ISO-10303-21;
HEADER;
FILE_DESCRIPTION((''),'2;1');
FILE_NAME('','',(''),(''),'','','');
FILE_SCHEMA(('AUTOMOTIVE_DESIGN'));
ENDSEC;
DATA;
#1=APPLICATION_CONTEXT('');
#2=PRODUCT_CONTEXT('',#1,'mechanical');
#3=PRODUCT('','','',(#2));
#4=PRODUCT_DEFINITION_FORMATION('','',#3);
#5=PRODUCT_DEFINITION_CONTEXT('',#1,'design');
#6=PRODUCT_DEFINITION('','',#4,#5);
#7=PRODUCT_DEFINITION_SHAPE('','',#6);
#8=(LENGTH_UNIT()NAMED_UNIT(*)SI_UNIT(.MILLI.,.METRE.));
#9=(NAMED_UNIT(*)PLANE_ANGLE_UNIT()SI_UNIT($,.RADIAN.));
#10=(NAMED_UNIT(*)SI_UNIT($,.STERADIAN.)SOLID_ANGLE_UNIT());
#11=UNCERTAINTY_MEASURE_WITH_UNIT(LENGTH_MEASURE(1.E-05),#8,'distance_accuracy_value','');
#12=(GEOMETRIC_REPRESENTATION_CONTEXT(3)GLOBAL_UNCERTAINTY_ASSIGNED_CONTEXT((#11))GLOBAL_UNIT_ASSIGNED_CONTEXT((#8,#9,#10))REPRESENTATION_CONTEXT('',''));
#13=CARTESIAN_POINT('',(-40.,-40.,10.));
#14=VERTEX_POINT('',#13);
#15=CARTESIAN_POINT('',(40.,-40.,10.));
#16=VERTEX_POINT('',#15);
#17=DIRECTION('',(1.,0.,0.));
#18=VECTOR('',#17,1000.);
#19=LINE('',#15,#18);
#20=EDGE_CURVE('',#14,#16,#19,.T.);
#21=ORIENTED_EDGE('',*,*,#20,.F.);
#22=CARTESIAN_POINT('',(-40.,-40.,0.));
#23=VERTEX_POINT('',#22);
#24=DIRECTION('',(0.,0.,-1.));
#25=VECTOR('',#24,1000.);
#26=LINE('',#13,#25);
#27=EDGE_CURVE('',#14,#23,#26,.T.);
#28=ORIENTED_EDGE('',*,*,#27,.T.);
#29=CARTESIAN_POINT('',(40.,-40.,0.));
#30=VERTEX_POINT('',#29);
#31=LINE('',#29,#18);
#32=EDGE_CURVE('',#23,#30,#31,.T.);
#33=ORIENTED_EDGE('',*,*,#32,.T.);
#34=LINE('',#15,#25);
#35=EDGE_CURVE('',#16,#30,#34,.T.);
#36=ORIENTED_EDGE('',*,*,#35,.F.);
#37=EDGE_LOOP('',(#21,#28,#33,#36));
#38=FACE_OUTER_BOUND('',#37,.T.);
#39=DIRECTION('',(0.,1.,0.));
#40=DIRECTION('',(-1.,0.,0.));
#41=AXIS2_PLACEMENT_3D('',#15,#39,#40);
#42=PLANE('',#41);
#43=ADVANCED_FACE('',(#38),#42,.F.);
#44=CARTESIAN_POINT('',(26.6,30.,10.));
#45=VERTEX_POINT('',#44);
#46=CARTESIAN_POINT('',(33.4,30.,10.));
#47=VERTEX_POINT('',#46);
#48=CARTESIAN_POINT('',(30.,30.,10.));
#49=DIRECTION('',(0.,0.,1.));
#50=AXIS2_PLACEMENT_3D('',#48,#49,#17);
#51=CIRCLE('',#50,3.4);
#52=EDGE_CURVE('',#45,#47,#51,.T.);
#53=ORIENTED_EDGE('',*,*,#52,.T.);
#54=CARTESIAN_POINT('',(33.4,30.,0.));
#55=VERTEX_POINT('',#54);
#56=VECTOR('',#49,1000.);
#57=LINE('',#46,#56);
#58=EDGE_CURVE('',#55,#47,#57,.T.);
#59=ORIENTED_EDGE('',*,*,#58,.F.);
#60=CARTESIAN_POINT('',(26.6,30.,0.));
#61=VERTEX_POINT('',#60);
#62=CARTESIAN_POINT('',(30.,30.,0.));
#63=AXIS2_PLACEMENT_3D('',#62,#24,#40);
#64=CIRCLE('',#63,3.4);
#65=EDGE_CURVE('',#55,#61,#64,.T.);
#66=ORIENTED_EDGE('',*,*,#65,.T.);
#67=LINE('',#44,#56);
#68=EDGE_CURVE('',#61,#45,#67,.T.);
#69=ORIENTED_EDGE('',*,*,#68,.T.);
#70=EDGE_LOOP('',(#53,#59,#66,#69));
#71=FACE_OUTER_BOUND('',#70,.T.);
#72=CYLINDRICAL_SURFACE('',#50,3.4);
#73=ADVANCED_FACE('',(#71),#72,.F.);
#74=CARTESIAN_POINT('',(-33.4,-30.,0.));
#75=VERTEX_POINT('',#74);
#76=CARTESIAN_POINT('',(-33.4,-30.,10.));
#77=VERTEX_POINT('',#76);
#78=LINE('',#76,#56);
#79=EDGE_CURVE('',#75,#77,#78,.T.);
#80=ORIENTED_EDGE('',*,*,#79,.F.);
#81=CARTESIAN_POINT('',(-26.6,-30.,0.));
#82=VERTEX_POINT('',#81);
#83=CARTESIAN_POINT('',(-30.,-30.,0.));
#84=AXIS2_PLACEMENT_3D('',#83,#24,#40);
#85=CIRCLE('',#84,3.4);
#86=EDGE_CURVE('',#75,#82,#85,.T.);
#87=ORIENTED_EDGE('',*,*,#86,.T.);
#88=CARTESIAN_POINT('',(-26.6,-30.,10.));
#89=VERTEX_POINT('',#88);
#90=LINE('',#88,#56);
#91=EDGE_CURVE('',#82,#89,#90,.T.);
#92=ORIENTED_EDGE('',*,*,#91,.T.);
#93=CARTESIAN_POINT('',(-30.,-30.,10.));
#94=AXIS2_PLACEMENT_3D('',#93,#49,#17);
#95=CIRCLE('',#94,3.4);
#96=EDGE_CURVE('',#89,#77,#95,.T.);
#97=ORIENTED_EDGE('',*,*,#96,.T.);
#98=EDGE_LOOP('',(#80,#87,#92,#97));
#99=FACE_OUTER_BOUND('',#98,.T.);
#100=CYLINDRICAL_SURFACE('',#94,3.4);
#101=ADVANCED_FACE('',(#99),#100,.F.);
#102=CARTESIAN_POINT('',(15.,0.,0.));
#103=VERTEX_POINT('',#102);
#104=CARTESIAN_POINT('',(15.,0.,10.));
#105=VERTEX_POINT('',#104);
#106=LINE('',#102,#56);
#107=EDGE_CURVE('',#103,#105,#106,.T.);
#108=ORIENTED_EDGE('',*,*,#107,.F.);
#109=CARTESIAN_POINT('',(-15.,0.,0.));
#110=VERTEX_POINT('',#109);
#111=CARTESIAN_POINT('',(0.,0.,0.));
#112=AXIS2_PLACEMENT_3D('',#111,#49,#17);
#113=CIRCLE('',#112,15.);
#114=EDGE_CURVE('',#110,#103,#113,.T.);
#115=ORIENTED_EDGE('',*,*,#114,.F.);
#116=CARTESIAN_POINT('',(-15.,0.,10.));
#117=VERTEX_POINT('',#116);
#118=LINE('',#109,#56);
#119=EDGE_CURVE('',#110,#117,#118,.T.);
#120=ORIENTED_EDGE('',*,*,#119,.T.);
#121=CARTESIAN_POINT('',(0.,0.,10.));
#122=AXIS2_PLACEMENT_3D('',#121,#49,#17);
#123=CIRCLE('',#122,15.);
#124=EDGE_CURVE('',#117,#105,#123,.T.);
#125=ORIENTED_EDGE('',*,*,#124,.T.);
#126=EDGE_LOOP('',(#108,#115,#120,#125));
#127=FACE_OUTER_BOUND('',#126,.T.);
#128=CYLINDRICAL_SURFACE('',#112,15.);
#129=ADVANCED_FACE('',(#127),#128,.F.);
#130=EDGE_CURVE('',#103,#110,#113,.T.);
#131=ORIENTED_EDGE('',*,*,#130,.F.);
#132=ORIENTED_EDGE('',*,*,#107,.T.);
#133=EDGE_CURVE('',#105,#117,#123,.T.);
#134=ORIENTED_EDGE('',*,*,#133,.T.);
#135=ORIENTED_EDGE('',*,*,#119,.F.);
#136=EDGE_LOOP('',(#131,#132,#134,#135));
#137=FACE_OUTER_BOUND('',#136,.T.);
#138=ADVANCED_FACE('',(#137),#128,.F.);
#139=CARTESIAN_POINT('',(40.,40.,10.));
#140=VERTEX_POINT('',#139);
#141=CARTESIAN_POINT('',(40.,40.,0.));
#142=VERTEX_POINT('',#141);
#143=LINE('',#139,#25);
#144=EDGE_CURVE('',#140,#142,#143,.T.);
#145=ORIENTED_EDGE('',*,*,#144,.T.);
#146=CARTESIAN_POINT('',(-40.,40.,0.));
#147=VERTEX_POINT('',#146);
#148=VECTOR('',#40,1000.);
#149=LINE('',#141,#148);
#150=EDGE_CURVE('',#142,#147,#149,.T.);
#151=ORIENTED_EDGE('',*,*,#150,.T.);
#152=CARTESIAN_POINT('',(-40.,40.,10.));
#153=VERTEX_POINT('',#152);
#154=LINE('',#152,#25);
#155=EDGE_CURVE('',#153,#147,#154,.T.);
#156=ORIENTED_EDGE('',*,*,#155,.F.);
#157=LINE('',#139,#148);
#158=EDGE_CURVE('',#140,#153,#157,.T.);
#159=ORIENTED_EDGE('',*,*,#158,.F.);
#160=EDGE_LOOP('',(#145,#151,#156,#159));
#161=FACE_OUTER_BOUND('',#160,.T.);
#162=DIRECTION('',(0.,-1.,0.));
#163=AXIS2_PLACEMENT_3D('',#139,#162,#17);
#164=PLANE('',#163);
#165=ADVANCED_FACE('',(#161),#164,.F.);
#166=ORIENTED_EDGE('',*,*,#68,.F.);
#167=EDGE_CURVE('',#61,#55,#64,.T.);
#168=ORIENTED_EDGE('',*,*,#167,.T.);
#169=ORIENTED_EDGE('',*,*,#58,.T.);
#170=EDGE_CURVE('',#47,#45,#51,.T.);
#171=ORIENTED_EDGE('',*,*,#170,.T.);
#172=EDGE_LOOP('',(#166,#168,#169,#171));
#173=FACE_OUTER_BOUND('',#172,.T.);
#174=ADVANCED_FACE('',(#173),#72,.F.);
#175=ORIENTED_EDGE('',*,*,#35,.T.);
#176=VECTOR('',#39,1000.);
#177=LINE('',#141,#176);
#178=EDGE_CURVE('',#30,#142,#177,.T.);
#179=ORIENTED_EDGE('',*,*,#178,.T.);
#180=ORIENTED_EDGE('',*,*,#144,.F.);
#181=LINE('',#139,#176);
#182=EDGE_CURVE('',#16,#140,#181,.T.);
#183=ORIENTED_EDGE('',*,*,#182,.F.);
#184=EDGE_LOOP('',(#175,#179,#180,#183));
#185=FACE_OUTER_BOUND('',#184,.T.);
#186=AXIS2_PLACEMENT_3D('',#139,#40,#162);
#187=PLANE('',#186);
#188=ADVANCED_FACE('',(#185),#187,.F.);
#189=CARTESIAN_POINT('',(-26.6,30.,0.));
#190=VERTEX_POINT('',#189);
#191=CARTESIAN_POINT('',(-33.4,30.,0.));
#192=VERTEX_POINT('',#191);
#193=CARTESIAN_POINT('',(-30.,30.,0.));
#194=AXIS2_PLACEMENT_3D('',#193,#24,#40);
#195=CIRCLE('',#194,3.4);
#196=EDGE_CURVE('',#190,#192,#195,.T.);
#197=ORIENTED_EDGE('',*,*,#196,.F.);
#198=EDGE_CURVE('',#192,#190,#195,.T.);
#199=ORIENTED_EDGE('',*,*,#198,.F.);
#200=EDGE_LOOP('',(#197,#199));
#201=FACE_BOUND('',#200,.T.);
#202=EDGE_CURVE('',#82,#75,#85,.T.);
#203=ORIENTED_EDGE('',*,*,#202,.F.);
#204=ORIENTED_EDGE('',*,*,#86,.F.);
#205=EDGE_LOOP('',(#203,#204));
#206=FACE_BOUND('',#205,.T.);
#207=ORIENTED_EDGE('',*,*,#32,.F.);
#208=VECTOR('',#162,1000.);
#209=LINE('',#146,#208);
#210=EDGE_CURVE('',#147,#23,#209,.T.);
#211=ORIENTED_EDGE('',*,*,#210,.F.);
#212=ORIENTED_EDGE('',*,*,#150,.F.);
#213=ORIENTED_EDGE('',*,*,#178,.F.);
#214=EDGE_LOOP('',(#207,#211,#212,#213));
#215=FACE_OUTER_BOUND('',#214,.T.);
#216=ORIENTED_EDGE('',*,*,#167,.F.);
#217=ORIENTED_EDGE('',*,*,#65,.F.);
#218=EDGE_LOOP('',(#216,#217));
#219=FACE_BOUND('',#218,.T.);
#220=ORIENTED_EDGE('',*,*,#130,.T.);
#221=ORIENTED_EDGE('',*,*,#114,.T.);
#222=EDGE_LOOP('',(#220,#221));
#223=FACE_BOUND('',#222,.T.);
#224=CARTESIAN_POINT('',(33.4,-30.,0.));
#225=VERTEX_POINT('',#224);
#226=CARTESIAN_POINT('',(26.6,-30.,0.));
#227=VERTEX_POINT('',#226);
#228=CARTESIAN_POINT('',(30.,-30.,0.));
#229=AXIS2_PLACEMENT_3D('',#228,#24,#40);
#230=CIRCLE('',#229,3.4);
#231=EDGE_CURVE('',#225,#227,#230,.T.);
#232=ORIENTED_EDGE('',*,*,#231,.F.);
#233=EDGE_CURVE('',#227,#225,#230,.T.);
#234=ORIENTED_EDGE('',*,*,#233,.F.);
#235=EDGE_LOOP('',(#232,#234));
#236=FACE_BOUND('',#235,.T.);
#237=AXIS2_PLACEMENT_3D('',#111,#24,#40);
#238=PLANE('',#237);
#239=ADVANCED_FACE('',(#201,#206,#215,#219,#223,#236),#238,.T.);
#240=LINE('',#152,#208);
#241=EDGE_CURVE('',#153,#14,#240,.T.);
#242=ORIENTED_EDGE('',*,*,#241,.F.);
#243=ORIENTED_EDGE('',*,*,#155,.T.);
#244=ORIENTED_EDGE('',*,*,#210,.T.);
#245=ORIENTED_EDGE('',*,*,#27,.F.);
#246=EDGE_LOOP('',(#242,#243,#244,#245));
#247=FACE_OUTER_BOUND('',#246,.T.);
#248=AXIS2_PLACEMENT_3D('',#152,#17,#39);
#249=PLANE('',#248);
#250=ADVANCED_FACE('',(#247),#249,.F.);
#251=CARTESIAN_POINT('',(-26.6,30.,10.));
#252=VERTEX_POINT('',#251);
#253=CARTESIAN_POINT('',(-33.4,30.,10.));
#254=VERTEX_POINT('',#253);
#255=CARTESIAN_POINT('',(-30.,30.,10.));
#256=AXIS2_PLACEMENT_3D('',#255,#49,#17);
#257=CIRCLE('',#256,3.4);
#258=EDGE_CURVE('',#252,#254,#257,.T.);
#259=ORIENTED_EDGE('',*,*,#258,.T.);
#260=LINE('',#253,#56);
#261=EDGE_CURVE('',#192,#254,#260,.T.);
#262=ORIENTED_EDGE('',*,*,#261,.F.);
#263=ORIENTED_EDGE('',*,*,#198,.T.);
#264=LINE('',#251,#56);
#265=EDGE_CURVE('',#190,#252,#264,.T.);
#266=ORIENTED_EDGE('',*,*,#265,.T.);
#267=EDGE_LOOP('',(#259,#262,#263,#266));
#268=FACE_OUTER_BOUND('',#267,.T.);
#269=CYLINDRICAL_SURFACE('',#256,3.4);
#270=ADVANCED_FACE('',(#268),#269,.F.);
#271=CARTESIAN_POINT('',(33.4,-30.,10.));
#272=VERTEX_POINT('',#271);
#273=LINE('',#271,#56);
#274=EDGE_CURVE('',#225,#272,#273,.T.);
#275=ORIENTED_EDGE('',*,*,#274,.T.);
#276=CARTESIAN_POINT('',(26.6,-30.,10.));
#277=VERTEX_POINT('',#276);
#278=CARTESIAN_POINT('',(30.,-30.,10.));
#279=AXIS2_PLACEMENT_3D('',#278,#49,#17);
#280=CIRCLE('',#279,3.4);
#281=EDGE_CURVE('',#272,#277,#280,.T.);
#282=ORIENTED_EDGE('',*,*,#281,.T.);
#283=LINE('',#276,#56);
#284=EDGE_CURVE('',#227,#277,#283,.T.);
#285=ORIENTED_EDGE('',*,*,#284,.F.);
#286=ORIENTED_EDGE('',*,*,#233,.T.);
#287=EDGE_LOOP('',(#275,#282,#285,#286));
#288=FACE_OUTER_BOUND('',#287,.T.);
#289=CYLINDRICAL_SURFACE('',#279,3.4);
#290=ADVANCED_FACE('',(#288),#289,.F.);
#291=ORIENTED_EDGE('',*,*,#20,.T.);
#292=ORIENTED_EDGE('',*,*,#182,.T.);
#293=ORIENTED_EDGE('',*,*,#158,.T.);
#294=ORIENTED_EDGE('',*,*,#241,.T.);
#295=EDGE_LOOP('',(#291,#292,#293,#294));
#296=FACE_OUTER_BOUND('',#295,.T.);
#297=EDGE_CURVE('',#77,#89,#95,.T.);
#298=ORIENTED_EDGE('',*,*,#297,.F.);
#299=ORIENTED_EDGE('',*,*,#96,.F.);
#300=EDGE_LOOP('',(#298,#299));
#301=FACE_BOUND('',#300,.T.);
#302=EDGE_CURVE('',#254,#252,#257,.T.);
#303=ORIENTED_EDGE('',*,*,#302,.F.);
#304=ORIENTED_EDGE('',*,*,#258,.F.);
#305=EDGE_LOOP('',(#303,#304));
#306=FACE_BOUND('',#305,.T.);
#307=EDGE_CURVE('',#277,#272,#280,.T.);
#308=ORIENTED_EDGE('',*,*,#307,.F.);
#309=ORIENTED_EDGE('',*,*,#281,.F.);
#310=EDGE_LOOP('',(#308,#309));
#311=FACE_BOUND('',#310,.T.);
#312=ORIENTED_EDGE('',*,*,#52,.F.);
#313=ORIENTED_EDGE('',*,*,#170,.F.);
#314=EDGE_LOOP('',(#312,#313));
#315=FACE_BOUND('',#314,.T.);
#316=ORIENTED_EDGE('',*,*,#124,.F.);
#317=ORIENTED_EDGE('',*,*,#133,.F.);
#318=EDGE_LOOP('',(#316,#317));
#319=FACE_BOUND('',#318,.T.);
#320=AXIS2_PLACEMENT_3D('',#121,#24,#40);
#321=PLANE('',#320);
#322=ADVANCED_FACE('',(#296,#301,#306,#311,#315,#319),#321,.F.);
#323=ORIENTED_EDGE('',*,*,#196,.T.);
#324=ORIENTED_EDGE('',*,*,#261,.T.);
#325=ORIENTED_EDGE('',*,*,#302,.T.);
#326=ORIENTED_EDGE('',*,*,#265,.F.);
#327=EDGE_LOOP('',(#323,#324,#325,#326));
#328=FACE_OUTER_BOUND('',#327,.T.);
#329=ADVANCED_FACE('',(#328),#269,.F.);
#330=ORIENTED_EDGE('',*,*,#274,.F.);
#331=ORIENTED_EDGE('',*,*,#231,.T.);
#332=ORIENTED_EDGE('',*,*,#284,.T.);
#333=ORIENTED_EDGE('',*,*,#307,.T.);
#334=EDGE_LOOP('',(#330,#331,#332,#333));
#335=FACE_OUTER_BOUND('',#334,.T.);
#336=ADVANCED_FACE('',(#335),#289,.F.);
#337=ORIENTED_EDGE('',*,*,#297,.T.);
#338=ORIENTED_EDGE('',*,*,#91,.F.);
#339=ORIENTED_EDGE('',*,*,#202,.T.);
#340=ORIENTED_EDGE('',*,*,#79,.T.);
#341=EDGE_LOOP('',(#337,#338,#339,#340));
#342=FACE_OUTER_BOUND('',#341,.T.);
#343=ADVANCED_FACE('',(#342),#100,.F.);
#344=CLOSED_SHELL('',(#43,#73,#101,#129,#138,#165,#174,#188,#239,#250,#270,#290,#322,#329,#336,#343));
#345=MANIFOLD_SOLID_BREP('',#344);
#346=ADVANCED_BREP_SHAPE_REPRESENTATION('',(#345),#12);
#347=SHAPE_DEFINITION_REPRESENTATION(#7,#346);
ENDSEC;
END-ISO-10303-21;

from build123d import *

# Parameters (mm, degrees)
SKETCH1_W             = 80
SKETCH1_H             = 80
BOSS_EXTRUDE1_DEPTH   = 10
M8_TAPPED_HOLE1_D     = 6.8
M8_TAPPED_HOLE1_DEPTH = 19.75
M8_TAPPED_HOLE1_TIP   = 2.042926105
SKETCH5_R             = 15
CUT_EXTRUDE1_DEPTH    = 10


with BuildPart() as part:
    # Sketch1 → Boss-Extrude1 (new body)
    with BuildSketch(Plane.XY):
        Rectangle(SKETCH1_W, SKETCH1_H)
    extrude(amount=BOSS_EXTRUDE1_DEPTH)

    # M8 Tapped Hole1
    with Locations(Plane.XY.offset(10)):
        with Locations((-30, 30), (30, 30), (30, -30), (-30, -30)):
            Hole(M8_TAPPED_HOLE1_D / 2, depth=M8_TAPPED_HOLE1_DEPTH)
            with Locations((0, 0, -(M8_TAPPED_HOLE1_DEPTH + M8_TAPPED_HOLE1_TIP / 2))):  # 118° drill point
                Cone(0, M8_TAPPED_HOLE1_D / 2, M8_TAPPED_HOLE1_TIP, mode=Mode.SUBTRACT)

    # Sketch5 → Cut-Extrude1 (cut)
    with BuildSketch(Plane.XY.offset(10)):
        Circle(SKETCH5_R)
    extrude(amount=-CUT_EXTRUDE1_DEPTH, mode=Mode.SUBTRACT)


solid = part.part
